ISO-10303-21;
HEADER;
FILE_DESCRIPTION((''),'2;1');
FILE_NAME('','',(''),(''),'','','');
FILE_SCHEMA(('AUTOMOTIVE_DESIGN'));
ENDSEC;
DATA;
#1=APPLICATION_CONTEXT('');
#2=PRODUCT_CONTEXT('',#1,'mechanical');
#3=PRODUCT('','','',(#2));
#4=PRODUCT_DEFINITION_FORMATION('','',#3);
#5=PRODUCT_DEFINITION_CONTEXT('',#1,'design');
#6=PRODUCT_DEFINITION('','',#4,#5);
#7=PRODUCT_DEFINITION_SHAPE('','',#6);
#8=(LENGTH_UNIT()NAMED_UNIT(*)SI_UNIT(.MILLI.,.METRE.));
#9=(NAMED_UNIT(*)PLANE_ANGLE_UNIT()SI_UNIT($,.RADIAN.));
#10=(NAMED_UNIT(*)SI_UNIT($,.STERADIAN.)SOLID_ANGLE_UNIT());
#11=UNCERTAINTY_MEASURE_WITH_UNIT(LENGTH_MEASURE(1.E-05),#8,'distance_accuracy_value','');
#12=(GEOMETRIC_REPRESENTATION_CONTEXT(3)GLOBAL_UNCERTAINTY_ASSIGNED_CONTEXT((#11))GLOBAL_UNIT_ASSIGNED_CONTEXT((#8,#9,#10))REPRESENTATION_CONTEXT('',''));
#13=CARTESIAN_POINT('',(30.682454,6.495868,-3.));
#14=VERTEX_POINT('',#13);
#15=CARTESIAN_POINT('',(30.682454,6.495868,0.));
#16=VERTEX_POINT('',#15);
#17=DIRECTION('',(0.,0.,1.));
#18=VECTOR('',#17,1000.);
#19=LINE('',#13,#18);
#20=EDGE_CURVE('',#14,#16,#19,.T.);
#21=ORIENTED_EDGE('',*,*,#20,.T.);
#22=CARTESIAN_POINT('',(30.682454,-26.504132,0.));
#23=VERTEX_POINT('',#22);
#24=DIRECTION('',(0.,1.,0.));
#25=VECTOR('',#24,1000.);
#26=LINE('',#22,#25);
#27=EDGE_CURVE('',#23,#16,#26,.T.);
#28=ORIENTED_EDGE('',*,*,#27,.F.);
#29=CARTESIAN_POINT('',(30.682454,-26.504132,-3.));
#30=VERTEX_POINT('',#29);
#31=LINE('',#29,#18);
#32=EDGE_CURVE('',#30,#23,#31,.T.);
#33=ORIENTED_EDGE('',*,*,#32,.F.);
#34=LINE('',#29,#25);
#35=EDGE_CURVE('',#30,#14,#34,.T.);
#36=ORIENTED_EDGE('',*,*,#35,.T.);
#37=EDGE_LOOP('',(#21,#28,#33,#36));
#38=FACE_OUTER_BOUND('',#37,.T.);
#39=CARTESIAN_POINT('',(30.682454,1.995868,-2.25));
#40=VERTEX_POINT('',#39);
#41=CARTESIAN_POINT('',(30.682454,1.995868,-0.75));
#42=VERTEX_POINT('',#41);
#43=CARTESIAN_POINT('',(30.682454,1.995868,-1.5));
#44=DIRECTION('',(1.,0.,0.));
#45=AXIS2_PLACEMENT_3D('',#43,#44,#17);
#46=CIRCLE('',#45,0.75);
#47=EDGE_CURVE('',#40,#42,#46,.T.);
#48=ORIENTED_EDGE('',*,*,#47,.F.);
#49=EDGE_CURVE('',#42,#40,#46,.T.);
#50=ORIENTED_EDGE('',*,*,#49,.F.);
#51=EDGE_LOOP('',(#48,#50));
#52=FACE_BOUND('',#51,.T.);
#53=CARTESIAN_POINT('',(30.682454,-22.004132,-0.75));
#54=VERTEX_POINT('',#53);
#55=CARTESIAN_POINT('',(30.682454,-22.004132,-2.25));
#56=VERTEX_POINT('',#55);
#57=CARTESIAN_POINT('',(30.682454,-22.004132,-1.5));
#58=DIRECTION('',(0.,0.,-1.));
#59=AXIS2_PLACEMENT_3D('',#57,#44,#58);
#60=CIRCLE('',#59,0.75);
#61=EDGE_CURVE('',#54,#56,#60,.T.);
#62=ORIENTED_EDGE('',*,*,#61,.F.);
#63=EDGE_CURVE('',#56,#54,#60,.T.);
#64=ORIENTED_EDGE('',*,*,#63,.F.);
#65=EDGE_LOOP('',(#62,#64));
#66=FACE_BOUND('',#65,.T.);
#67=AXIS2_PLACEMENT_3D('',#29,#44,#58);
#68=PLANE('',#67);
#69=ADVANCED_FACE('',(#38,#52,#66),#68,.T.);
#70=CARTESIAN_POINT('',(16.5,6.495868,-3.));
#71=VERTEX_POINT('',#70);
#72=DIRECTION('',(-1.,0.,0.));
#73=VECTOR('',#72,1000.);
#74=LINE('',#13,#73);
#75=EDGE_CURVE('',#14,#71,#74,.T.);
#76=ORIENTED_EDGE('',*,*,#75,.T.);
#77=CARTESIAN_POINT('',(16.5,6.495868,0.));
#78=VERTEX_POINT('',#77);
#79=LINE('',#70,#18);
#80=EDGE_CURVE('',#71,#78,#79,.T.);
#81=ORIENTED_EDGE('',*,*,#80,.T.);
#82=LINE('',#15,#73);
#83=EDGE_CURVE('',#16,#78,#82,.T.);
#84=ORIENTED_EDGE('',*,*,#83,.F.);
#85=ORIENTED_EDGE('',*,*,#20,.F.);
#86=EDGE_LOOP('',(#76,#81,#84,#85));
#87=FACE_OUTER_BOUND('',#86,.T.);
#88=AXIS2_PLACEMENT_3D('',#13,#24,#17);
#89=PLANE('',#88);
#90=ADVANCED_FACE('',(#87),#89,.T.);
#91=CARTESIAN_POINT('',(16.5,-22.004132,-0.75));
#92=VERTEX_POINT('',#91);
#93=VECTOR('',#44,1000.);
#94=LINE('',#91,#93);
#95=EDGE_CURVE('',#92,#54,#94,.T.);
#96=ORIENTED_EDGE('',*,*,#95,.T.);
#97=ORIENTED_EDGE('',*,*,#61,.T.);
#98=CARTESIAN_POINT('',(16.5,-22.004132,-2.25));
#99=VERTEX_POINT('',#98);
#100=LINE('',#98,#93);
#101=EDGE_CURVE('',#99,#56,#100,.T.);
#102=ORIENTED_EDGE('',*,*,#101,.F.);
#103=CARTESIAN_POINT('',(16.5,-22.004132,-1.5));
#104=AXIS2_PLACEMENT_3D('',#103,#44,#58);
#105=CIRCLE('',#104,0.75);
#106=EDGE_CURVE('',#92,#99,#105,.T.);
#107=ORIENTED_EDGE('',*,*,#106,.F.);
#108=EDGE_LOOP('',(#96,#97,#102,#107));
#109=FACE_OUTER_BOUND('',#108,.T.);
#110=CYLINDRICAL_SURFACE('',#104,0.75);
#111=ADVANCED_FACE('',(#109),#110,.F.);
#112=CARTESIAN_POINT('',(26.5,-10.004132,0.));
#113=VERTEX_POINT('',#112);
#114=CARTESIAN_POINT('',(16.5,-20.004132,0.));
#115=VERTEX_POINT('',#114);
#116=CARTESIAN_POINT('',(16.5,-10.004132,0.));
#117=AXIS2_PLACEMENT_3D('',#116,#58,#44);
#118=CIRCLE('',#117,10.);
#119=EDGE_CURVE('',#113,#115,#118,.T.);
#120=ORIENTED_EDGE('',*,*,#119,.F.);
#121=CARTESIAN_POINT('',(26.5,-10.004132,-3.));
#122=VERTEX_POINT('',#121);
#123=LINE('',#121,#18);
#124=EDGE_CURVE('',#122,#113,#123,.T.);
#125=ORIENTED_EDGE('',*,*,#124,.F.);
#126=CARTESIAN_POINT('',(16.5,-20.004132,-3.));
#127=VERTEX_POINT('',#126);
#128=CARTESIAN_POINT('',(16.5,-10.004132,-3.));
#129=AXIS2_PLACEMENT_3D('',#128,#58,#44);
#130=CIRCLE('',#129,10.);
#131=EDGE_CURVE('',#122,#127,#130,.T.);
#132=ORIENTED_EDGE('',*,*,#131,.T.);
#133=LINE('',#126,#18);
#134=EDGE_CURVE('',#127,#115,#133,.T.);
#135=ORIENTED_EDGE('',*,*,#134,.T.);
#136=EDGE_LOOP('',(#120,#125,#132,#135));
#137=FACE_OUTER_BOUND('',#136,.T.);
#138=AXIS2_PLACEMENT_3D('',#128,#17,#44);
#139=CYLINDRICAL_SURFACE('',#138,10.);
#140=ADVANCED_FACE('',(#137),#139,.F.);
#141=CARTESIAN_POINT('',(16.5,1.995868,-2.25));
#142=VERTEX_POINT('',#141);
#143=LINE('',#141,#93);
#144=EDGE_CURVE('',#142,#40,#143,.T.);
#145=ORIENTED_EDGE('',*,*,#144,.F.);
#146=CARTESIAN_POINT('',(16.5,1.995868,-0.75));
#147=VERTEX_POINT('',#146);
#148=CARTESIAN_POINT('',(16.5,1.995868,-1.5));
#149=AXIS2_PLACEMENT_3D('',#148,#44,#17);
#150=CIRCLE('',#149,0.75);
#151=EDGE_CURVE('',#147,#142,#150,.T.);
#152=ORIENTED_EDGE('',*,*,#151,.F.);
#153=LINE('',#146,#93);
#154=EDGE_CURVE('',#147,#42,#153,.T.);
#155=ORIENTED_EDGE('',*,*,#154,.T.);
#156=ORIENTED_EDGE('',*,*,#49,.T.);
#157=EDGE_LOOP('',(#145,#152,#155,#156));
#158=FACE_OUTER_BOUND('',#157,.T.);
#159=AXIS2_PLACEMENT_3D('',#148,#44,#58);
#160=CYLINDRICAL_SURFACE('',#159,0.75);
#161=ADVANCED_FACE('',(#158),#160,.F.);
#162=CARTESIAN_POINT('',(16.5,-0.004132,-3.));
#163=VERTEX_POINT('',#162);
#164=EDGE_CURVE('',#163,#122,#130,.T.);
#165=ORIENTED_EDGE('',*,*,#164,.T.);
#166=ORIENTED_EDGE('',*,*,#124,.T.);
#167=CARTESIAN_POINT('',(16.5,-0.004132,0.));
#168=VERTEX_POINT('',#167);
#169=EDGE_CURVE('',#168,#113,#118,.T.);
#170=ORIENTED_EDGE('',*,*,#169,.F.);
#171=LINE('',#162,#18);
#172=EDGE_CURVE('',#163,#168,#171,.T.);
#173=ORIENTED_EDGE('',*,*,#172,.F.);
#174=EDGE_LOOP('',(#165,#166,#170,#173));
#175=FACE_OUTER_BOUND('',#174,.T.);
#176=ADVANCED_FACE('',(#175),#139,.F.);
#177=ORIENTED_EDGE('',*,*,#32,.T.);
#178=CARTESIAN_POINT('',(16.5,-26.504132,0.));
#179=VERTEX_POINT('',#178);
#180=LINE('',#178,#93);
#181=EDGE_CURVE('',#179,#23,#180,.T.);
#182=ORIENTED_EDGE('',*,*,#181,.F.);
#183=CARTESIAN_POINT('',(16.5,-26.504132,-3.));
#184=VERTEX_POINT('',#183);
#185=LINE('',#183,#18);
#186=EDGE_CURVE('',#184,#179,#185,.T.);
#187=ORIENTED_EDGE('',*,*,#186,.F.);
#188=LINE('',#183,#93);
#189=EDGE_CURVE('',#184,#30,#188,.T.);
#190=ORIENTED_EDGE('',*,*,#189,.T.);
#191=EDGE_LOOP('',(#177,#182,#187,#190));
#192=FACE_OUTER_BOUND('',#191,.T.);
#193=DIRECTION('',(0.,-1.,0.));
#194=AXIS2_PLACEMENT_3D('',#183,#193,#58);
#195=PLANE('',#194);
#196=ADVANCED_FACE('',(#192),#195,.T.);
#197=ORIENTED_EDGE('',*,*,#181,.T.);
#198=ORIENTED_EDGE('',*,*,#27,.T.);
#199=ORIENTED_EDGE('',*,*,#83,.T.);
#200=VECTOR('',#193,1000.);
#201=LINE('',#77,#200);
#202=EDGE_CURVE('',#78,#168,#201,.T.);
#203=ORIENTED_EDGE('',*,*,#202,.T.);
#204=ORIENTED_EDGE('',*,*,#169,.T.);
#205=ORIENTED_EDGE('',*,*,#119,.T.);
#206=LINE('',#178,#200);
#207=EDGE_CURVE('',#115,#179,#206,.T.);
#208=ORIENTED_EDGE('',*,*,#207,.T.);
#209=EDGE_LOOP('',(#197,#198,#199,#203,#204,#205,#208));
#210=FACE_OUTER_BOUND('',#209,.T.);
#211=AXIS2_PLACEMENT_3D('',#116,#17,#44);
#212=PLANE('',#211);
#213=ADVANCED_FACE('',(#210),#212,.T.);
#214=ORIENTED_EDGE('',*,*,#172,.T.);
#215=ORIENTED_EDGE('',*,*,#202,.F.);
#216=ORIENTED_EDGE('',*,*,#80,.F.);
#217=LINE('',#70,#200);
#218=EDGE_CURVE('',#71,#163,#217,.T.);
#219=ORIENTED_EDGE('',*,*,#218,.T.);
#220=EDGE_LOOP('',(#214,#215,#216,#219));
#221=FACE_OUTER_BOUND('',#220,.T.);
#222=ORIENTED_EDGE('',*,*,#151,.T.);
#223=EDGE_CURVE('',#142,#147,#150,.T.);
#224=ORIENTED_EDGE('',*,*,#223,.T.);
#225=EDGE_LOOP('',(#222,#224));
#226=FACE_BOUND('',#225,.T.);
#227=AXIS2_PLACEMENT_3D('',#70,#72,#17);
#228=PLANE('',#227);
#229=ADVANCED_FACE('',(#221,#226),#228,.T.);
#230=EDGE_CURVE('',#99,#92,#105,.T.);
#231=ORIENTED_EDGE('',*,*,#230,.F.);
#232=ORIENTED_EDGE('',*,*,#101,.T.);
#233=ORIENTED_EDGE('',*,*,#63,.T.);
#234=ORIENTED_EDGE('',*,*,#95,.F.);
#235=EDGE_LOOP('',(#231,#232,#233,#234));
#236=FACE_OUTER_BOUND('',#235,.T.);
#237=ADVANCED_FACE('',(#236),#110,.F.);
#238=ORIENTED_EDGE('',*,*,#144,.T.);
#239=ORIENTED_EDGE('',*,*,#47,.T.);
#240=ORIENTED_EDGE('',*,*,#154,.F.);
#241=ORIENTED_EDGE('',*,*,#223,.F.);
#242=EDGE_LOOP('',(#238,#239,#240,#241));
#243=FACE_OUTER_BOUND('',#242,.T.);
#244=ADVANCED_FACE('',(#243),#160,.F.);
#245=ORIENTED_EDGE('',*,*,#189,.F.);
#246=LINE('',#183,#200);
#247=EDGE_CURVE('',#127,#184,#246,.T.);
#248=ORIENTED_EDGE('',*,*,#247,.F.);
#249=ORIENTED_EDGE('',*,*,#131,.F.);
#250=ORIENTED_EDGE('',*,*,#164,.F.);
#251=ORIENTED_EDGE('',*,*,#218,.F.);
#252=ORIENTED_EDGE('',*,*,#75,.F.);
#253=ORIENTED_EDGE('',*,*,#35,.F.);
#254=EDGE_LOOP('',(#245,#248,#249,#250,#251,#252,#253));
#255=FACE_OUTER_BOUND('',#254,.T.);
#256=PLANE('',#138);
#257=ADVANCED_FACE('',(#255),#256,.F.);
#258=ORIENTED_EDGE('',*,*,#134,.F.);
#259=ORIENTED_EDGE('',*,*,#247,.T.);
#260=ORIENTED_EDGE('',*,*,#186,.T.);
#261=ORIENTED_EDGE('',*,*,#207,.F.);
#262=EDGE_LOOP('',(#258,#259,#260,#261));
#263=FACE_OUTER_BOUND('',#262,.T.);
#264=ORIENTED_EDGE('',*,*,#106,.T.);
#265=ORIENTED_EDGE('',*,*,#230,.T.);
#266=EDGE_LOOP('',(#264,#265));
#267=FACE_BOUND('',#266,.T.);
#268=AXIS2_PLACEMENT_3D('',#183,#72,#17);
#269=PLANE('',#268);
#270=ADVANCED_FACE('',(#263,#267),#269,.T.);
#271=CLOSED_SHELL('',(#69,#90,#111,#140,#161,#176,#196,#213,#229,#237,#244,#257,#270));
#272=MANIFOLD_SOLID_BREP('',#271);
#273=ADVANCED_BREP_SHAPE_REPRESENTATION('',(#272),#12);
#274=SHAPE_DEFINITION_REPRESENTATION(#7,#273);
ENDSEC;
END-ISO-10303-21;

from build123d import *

# Parameters (mm, degrees)
BOSS_EXTRUDE1_DEPTH = 3
SKETCH3_R           = 0.75
CUT_EXTRUDE1_DEPTH  = 31.209452006


with BuildPart() as part:
    # Sketch2 → Boss-Extrude1 (new body)
    with BuildSketch(Plane.XY):
        with BuildLine():
            Line((16.5, -26.504131531), (30.682454029, -26.504131531))
            Line((30.682454029, -26.504131531), (30.682454029, 6.495868469))
            Line((30.682454029, 6.495868469), (16.5, 6.495868469))
            Line((16.5, 6.495868469), (16.5, -0.004131531))
            ThreePointArc((16.5, -0.004131531), (26.5, -10.004131531), (16.5, -20.004131531))
            Line((16.5, -20.004131531), (16.5, -26.504131531))
        make_face()
    extrude(amount=-BOSS_EXTRUDE1_DEPTH)

    # Sketch3 → Cut-Extrude1 (cut, through all)
    with BuildSketch(Plane(origin=(30.682454029, 0, 0), x_dir=(0, 0, -1), z_dir=(1, 0, 0))):
        with Locations((1.5, -22.004131531)):
            Circle(SKETCH3_R)
        with Locations(Location((1.5, 1.995868469, 0), (0, 0, 180))):
            Circle(SKETCH3_R)
    extrude(amount=-CUT_EXTRUDE1_DEPTH, mode=Mode.SUBTRACT)


solid = part.part
